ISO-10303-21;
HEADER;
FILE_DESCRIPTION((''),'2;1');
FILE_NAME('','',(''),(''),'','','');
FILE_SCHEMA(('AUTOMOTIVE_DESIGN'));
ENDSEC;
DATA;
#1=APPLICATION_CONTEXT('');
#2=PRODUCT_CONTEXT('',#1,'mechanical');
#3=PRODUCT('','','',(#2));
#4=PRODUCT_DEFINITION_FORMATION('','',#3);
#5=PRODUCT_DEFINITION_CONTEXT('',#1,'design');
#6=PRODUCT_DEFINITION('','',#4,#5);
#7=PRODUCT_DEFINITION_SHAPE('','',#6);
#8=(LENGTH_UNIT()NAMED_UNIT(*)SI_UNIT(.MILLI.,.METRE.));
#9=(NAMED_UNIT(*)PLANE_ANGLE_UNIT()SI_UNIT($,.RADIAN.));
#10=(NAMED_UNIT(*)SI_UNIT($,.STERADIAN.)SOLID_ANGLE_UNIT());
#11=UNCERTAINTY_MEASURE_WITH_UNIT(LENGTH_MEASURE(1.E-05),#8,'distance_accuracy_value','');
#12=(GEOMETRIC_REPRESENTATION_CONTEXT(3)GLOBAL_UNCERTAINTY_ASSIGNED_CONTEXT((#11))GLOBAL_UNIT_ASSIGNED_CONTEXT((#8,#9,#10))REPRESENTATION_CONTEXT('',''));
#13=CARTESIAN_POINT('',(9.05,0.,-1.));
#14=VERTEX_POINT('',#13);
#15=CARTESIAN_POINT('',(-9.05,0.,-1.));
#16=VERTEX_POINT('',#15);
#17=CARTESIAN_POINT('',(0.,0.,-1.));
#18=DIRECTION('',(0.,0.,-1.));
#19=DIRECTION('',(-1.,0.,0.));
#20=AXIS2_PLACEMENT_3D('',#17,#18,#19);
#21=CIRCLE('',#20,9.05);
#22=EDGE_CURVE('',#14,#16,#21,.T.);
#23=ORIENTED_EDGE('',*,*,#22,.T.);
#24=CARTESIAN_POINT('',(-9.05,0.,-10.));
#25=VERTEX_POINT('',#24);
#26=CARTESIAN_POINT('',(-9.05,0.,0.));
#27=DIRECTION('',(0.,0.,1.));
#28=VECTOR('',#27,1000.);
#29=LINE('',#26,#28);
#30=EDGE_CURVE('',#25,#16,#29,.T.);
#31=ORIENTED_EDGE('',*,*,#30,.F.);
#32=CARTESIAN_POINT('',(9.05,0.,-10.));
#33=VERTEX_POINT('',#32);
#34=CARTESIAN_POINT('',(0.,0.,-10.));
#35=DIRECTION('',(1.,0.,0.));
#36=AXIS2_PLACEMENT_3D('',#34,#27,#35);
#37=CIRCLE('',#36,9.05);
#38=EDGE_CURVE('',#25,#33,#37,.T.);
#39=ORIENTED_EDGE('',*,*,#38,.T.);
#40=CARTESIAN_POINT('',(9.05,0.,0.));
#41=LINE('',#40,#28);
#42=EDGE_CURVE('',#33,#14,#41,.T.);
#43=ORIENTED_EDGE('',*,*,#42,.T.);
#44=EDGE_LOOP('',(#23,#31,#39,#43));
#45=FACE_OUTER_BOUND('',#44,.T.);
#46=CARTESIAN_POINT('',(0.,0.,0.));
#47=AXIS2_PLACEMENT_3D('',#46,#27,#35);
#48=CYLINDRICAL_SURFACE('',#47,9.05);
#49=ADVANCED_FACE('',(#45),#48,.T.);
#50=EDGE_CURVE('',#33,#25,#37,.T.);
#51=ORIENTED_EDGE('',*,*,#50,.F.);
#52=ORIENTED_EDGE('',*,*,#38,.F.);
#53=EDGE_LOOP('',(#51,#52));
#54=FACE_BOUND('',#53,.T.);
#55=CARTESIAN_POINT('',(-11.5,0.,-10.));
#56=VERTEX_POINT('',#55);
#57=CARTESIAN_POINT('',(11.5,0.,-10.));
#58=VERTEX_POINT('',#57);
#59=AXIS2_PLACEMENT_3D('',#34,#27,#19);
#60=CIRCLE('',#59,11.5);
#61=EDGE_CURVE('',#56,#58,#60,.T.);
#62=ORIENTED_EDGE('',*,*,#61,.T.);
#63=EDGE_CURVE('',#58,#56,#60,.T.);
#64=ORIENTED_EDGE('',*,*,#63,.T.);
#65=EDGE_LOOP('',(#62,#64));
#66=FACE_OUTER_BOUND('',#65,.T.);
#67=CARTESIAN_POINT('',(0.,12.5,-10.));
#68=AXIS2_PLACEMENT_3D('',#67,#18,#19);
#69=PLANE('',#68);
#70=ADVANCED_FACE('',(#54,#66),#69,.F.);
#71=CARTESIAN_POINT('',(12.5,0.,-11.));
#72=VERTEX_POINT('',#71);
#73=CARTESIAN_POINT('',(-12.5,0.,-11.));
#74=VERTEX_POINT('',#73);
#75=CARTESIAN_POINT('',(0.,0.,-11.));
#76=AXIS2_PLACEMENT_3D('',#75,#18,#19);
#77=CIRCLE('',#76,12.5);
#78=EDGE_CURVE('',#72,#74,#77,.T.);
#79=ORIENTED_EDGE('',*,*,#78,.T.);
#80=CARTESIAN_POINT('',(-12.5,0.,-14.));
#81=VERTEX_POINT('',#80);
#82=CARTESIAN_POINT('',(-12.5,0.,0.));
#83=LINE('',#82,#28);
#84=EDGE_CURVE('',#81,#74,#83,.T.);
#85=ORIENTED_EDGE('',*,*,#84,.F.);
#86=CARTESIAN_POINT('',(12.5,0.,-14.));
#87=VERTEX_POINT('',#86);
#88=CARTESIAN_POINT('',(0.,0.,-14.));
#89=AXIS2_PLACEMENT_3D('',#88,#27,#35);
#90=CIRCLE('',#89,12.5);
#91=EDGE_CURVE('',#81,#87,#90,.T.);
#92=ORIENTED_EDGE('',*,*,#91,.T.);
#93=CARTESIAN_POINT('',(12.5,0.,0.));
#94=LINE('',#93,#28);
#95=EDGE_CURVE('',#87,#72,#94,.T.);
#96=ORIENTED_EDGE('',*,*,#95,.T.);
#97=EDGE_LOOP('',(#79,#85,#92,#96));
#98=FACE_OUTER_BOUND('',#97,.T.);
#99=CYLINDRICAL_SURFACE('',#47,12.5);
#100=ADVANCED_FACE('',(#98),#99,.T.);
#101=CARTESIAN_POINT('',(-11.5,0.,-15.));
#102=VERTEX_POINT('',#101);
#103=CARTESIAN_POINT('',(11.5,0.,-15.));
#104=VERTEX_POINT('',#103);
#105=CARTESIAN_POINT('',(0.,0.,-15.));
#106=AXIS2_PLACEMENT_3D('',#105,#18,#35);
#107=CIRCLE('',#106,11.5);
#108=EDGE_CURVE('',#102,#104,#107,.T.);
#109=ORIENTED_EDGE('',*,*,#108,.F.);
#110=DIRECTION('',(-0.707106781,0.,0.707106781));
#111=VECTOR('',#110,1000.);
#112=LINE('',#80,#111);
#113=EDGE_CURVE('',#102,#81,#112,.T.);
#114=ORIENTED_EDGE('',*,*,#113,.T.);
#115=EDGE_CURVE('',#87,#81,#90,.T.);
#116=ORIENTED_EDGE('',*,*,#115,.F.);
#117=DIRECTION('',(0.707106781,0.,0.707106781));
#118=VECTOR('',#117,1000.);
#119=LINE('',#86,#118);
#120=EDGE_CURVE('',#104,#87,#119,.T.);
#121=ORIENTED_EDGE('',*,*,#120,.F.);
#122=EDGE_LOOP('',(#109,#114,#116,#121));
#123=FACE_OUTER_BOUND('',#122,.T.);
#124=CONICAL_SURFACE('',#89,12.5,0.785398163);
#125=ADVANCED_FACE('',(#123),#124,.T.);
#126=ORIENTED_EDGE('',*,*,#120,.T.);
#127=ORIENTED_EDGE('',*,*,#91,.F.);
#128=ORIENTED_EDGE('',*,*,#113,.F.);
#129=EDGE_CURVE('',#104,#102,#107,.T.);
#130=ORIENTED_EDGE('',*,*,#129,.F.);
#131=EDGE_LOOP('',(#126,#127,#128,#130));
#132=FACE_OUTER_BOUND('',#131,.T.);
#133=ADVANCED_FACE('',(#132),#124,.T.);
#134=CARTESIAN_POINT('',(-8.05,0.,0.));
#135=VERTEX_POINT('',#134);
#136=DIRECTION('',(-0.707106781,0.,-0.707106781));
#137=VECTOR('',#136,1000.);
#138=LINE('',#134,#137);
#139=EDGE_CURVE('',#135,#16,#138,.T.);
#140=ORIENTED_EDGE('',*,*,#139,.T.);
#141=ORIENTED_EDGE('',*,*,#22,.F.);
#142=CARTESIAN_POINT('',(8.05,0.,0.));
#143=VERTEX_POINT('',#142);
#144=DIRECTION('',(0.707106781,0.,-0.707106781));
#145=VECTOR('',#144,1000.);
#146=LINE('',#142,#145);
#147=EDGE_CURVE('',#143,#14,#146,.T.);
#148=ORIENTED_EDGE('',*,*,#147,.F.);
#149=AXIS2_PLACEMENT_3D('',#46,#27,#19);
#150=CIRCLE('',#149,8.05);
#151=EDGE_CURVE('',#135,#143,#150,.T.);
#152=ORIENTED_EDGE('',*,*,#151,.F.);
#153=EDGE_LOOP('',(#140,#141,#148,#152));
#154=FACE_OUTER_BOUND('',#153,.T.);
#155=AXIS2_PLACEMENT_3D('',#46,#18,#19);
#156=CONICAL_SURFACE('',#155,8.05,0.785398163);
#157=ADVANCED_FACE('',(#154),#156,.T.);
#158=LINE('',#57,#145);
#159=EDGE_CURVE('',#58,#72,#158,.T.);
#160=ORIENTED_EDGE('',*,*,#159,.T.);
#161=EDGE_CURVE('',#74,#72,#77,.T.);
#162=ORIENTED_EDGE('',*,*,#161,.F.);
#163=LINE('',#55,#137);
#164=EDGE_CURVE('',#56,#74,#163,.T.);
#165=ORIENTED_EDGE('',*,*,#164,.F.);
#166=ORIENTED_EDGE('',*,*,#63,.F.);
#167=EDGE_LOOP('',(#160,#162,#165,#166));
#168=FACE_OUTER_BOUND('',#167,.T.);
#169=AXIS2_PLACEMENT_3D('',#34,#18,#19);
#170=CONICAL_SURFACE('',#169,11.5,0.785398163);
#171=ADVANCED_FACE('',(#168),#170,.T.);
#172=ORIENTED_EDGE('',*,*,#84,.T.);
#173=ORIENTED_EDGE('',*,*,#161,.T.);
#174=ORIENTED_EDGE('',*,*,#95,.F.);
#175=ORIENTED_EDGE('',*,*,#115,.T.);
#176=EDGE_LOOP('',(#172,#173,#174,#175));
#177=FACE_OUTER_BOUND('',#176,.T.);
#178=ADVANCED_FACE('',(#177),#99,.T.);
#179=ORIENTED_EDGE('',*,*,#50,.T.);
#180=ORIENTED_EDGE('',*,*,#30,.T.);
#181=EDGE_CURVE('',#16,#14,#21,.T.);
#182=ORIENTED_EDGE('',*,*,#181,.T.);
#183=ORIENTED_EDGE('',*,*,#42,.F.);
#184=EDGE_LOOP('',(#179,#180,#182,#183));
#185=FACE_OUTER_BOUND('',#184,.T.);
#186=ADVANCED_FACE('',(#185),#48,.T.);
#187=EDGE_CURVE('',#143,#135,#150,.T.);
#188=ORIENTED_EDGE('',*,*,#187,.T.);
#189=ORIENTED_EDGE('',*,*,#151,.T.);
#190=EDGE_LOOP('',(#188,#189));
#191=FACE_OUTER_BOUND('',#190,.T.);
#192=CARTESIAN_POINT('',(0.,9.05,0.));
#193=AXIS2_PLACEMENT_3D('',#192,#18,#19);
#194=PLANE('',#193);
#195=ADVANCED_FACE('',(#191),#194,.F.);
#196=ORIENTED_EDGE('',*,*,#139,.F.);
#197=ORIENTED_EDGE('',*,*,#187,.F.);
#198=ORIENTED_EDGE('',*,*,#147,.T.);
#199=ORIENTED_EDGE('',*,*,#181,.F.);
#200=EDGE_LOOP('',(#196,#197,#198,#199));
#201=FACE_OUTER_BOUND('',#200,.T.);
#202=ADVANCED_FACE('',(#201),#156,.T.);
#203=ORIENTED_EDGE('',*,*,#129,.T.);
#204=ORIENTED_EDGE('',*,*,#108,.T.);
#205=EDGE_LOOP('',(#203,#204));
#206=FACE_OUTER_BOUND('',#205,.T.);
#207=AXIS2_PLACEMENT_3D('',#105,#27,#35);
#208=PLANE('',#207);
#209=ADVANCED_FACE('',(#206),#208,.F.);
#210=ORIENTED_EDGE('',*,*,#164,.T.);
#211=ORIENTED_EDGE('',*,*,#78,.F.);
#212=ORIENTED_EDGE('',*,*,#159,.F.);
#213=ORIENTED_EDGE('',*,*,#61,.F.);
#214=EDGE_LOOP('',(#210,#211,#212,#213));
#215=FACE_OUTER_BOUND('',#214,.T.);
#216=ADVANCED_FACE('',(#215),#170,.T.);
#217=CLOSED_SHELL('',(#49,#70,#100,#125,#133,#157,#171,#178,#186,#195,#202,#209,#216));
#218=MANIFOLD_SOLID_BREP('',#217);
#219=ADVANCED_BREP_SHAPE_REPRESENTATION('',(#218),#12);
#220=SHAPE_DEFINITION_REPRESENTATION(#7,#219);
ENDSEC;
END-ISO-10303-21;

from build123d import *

# Parameters (mm, degrees)
CHAMFER1_SIZE = 1


with BuildPart() as part:
    # Sketch1 → Revolve1 (revolve)
    with BuildSketch(Plane(origin=(0, 0, 0), x_dir=(0, 0, -1), z_dir=(1, 0, 0)), mode=Mode.PRIVATE) as revolve1_sk:
        Polygon((15, 0), (15, 12.5), (10, 12.5), (10, 9.05), (0, 9.05), (0, 0), align=None)
    revolve(revolve1_sk.sketch.rotate(Axis((0, 0, 0), (0, 0, -1)), 90), axis=Axis((0, 0, 0), (0, 0, -1)))

    # Chamfer1
    chamfer1_edges = [part.edges().sort_by_distance(p)[0] for p in [
        (-9.05, 0, 0),
        (-12.5, 0, -10),
        (-12.5, 0, -15),
    ]]
    chamfer(chamfer1_edges, length=CHAMFER1_SIZE)


solid = part.part
